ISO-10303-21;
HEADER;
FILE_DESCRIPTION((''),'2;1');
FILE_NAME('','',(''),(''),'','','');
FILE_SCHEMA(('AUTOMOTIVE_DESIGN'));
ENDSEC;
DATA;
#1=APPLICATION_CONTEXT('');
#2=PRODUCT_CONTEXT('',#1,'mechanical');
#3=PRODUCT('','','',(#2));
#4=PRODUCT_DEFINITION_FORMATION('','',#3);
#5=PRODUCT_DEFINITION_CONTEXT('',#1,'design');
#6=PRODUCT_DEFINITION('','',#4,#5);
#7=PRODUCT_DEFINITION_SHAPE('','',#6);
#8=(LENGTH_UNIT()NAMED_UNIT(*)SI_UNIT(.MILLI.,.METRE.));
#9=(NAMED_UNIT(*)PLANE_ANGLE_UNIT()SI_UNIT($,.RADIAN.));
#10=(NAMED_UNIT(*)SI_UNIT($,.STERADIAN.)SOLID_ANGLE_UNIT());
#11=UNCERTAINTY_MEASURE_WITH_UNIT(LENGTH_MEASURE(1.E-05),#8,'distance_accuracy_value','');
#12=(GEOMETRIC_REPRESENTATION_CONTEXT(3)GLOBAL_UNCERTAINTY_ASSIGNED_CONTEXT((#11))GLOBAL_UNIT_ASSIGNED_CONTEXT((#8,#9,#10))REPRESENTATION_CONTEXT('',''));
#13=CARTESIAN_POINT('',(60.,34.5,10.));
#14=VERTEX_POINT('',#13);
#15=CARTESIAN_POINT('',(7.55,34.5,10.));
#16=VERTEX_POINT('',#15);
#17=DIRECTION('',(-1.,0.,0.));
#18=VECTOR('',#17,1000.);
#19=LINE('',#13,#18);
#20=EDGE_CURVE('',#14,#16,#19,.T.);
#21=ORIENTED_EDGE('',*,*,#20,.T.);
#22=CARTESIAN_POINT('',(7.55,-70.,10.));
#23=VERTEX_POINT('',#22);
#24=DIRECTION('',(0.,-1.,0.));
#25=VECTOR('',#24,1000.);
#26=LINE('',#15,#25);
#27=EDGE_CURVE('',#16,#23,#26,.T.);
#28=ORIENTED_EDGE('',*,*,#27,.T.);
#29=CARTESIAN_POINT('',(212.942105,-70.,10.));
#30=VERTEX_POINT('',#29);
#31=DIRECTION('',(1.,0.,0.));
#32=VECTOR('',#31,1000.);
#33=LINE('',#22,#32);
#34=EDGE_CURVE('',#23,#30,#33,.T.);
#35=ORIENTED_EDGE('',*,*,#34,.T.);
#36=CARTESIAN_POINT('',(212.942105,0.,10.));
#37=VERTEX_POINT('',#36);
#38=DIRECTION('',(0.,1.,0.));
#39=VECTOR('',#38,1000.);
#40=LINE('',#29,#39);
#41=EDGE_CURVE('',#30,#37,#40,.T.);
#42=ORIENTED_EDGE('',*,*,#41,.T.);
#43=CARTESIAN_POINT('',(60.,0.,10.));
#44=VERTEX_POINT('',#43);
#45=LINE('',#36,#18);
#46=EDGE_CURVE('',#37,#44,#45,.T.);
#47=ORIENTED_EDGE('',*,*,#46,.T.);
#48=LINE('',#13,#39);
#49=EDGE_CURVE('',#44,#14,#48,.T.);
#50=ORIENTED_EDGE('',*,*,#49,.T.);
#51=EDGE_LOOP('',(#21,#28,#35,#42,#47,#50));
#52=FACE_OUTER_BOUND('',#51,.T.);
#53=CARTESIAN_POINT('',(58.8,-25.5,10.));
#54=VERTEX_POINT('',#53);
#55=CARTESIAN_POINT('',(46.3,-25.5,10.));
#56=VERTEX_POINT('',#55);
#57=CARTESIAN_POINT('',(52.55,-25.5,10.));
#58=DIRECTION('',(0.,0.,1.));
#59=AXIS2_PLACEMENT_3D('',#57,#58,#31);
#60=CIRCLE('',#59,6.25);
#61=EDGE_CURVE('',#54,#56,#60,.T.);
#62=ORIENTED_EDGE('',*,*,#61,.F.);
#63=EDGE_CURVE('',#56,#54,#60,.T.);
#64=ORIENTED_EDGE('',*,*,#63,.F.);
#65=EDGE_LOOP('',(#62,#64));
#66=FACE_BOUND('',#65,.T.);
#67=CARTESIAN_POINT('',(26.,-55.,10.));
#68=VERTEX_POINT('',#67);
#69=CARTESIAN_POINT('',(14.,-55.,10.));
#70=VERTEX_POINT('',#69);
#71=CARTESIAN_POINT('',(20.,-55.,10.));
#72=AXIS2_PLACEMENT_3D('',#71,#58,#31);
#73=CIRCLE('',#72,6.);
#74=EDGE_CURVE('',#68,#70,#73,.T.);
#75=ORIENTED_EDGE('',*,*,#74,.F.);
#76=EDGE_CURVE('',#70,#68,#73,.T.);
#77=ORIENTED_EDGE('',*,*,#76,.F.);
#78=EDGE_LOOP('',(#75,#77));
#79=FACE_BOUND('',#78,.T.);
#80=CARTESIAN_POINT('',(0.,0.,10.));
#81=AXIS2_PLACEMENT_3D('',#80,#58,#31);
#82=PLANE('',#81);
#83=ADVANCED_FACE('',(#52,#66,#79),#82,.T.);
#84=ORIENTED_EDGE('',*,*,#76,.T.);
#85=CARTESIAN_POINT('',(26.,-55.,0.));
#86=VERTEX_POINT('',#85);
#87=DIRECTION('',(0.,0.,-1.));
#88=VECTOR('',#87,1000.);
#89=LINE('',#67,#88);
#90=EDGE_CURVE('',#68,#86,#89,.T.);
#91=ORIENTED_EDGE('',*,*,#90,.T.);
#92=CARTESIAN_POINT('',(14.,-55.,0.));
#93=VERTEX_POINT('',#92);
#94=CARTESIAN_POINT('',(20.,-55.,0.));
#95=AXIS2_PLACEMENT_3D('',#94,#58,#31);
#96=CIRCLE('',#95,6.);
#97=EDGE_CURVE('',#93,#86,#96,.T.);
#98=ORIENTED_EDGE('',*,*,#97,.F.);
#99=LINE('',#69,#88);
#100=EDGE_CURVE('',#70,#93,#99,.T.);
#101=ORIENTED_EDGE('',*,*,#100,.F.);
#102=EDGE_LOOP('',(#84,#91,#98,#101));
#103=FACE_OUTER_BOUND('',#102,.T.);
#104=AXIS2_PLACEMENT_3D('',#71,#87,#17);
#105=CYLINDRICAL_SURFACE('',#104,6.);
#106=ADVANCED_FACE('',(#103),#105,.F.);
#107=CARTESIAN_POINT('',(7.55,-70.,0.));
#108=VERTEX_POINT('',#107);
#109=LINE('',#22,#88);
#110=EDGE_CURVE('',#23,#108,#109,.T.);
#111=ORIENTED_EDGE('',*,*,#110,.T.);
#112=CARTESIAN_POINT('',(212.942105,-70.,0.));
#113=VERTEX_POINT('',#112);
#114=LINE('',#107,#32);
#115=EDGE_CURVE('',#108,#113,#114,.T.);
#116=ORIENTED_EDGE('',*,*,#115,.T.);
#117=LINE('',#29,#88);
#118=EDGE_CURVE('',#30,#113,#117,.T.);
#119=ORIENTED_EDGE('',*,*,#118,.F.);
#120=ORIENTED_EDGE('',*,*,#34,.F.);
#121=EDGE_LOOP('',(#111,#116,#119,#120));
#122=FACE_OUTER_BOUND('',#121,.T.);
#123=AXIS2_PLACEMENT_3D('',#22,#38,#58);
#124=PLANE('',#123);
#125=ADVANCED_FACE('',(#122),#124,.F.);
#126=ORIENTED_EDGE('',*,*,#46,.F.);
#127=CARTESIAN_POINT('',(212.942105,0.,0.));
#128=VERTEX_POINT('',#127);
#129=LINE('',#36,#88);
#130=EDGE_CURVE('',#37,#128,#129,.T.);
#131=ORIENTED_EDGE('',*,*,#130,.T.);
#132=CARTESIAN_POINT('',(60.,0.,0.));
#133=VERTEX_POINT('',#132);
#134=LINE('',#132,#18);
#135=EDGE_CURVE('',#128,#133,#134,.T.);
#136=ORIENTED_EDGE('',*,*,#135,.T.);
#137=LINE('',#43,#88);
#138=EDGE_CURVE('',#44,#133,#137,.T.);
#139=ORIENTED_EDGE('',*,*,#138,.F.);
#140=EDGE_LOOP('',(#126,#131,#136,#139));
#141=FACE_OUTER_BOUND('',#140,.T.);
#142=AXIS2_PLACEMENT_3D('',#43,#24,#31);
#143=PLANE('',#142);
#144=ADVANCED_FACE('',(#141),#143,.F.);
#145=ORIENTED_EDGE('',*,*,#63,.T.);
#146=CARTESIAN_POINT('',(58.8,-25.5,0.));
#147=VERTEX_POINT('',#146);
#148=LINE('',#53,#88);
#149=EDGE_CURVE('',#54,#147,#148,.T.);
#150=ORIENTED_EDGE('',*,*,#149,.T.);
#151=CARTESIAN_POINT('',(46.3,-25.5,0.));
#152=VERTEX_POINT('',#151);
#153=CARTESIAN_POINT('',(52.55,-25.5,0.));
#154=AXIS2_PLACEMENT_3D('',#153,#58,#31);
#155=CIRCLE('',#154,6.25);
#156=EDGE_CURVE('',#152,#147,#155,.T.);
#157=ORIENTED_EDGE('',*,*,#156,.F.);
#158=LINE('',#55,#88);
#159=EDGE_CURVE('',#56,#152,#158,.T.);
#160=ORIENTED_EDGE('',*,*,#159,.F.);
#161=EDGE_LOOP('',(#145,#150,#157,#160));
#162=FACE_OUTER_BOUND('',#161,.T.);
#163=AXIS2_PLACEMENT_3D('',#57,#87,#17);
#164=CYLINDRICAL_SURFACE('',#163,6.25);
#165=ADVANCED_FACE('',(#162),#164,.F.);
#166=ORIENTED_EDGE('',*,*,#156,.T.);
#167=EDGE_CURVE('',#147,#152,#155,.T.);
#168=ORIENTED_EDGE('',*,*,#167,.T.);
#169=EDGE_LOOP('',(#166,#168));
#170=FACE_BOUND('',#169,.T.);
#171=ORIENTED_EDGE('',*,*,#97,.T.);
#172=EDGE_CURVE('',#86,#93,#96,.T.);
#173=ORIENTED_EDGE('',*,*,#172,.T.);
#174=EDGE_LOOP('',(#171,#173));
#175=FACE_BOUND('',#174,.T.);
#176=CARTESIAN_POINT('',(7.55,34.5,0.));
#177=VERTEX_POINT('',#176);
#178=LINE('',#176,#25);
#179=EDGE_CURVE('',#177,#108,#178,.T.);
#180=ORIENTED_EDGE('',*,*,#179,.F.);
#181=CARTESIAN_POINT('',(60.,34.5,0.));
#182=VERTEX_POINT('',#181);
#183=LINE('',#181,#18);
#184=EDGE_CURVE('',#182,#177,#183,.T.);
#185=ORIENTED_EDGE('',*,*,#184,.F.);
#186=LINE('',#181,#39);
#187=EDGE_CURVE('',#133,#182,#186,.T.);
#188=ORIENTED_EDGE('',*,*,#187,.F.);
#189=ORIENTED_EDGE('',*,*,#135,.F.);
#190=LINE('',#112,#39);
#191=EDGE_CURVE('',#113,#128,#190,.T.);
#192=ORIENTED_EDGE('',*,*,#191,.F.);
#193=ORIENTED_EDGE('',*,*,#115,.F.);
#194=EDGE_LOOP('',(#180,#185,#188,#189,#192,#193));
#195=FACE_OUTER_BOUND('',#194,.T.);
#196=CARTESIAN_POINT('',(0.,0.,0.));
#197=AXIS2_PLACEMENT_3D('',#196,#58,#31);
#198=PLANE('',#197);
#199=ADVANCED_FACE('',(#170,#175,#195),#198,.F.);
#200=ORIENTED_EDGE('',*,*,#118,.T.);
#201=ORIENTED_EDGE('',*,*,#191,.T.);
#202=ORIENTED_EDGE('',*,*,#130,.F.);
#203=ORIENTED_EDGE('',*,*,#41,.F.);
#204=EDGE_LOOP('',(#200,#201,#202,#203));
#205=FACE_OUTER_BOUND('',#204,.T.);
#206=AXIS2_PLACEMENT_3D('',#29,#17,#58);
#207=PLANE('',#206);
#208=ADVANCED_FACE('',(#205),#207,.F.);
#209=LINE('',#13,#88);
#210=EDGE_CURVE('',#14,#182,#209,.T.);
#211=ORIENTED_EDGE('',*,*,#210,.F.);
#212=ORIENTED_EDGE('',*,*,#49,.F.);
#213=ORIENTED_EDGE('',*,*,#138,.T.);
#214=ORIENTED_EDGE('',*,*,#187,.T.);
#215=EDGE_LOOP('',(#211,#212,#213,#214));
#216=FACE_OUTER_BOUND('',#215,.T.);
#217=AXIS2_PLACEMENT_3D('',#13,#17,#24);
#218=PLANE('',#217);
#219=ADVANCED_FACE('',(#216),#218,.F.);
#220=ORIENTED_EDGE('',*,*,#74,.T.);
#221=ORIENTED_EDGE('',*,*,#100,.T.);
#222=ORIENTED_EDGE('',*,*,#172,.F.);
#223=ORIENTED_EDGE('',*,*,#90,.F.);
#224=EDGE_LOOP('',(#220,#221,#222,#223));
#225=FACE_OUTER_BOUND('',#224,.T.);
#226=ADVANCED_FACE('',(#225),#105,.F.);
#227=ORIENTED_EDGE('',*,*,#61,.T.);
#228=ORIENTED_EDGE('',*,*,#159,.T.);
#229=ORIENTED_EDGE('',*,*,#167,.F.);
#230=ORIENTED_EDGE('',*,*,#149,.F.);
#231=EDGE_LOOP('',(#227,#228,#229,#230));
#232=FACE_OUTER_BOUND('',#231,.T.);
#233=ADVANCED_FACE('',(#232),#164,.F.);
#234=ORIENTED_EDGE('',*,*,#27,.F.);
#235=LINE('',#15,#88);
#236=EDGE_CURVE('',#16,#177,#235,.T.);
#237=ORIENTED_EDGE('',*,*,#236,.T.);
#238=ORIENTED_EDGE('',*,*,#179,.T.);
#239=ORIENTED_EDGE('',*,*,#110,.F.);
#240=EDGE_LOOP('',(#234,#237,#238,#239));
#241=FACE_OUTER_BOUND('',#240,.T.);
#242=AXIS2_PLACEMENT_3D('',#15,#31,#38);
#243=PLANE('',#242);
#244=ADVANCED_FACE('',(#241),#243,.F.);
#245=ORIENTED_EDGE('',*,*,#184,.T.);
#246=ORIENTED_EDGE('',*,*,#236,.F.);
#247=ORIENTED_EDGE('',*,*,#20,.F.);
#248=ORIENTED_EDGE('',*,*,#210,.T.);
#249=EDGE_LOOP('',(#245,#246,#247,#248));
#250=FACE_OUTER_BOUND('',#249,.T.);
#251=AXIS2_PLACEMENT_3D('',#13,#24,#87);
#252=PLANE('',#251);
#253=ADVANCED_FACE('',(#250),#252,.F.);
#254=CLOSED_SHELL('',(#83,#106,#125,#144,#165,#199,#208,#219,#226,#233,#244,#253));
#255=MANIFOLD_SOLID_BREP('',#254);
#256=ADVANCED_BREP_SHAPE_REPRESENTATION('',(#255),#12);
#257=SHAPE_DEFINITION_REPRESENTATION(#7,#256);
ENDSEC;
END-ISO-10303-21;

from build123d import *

# Parameters (mm, degrees)
SKETCH1_R           = 6
SKETCH1_R_2         = 6.25
BOSS_EXTRUDE1_DEPTH = 10


with BuildPart() as part:
    # Sketch1 → Boss-Extrude1 (new body)
    with BuildSketch(Plane.XY):
        Polygon((7.55, 34.5), (7.55, -70), (212.942105032, -70), (212.942105032, 0), (137.727272727, 0), (60, 0), (60, 34.5), align=None)
        with Locations((20, -55)):
            Circle(SKETCH1_R, mode=Mode.SUBTRACT)
        with Locations((52.55, -25.5)):
            Circle(SKETCH1_R_2, mode=Mode.SUBTRACT)
    extrude(amount=BOSS_EXTRUDE1_DEPTH)


solid = part.part
